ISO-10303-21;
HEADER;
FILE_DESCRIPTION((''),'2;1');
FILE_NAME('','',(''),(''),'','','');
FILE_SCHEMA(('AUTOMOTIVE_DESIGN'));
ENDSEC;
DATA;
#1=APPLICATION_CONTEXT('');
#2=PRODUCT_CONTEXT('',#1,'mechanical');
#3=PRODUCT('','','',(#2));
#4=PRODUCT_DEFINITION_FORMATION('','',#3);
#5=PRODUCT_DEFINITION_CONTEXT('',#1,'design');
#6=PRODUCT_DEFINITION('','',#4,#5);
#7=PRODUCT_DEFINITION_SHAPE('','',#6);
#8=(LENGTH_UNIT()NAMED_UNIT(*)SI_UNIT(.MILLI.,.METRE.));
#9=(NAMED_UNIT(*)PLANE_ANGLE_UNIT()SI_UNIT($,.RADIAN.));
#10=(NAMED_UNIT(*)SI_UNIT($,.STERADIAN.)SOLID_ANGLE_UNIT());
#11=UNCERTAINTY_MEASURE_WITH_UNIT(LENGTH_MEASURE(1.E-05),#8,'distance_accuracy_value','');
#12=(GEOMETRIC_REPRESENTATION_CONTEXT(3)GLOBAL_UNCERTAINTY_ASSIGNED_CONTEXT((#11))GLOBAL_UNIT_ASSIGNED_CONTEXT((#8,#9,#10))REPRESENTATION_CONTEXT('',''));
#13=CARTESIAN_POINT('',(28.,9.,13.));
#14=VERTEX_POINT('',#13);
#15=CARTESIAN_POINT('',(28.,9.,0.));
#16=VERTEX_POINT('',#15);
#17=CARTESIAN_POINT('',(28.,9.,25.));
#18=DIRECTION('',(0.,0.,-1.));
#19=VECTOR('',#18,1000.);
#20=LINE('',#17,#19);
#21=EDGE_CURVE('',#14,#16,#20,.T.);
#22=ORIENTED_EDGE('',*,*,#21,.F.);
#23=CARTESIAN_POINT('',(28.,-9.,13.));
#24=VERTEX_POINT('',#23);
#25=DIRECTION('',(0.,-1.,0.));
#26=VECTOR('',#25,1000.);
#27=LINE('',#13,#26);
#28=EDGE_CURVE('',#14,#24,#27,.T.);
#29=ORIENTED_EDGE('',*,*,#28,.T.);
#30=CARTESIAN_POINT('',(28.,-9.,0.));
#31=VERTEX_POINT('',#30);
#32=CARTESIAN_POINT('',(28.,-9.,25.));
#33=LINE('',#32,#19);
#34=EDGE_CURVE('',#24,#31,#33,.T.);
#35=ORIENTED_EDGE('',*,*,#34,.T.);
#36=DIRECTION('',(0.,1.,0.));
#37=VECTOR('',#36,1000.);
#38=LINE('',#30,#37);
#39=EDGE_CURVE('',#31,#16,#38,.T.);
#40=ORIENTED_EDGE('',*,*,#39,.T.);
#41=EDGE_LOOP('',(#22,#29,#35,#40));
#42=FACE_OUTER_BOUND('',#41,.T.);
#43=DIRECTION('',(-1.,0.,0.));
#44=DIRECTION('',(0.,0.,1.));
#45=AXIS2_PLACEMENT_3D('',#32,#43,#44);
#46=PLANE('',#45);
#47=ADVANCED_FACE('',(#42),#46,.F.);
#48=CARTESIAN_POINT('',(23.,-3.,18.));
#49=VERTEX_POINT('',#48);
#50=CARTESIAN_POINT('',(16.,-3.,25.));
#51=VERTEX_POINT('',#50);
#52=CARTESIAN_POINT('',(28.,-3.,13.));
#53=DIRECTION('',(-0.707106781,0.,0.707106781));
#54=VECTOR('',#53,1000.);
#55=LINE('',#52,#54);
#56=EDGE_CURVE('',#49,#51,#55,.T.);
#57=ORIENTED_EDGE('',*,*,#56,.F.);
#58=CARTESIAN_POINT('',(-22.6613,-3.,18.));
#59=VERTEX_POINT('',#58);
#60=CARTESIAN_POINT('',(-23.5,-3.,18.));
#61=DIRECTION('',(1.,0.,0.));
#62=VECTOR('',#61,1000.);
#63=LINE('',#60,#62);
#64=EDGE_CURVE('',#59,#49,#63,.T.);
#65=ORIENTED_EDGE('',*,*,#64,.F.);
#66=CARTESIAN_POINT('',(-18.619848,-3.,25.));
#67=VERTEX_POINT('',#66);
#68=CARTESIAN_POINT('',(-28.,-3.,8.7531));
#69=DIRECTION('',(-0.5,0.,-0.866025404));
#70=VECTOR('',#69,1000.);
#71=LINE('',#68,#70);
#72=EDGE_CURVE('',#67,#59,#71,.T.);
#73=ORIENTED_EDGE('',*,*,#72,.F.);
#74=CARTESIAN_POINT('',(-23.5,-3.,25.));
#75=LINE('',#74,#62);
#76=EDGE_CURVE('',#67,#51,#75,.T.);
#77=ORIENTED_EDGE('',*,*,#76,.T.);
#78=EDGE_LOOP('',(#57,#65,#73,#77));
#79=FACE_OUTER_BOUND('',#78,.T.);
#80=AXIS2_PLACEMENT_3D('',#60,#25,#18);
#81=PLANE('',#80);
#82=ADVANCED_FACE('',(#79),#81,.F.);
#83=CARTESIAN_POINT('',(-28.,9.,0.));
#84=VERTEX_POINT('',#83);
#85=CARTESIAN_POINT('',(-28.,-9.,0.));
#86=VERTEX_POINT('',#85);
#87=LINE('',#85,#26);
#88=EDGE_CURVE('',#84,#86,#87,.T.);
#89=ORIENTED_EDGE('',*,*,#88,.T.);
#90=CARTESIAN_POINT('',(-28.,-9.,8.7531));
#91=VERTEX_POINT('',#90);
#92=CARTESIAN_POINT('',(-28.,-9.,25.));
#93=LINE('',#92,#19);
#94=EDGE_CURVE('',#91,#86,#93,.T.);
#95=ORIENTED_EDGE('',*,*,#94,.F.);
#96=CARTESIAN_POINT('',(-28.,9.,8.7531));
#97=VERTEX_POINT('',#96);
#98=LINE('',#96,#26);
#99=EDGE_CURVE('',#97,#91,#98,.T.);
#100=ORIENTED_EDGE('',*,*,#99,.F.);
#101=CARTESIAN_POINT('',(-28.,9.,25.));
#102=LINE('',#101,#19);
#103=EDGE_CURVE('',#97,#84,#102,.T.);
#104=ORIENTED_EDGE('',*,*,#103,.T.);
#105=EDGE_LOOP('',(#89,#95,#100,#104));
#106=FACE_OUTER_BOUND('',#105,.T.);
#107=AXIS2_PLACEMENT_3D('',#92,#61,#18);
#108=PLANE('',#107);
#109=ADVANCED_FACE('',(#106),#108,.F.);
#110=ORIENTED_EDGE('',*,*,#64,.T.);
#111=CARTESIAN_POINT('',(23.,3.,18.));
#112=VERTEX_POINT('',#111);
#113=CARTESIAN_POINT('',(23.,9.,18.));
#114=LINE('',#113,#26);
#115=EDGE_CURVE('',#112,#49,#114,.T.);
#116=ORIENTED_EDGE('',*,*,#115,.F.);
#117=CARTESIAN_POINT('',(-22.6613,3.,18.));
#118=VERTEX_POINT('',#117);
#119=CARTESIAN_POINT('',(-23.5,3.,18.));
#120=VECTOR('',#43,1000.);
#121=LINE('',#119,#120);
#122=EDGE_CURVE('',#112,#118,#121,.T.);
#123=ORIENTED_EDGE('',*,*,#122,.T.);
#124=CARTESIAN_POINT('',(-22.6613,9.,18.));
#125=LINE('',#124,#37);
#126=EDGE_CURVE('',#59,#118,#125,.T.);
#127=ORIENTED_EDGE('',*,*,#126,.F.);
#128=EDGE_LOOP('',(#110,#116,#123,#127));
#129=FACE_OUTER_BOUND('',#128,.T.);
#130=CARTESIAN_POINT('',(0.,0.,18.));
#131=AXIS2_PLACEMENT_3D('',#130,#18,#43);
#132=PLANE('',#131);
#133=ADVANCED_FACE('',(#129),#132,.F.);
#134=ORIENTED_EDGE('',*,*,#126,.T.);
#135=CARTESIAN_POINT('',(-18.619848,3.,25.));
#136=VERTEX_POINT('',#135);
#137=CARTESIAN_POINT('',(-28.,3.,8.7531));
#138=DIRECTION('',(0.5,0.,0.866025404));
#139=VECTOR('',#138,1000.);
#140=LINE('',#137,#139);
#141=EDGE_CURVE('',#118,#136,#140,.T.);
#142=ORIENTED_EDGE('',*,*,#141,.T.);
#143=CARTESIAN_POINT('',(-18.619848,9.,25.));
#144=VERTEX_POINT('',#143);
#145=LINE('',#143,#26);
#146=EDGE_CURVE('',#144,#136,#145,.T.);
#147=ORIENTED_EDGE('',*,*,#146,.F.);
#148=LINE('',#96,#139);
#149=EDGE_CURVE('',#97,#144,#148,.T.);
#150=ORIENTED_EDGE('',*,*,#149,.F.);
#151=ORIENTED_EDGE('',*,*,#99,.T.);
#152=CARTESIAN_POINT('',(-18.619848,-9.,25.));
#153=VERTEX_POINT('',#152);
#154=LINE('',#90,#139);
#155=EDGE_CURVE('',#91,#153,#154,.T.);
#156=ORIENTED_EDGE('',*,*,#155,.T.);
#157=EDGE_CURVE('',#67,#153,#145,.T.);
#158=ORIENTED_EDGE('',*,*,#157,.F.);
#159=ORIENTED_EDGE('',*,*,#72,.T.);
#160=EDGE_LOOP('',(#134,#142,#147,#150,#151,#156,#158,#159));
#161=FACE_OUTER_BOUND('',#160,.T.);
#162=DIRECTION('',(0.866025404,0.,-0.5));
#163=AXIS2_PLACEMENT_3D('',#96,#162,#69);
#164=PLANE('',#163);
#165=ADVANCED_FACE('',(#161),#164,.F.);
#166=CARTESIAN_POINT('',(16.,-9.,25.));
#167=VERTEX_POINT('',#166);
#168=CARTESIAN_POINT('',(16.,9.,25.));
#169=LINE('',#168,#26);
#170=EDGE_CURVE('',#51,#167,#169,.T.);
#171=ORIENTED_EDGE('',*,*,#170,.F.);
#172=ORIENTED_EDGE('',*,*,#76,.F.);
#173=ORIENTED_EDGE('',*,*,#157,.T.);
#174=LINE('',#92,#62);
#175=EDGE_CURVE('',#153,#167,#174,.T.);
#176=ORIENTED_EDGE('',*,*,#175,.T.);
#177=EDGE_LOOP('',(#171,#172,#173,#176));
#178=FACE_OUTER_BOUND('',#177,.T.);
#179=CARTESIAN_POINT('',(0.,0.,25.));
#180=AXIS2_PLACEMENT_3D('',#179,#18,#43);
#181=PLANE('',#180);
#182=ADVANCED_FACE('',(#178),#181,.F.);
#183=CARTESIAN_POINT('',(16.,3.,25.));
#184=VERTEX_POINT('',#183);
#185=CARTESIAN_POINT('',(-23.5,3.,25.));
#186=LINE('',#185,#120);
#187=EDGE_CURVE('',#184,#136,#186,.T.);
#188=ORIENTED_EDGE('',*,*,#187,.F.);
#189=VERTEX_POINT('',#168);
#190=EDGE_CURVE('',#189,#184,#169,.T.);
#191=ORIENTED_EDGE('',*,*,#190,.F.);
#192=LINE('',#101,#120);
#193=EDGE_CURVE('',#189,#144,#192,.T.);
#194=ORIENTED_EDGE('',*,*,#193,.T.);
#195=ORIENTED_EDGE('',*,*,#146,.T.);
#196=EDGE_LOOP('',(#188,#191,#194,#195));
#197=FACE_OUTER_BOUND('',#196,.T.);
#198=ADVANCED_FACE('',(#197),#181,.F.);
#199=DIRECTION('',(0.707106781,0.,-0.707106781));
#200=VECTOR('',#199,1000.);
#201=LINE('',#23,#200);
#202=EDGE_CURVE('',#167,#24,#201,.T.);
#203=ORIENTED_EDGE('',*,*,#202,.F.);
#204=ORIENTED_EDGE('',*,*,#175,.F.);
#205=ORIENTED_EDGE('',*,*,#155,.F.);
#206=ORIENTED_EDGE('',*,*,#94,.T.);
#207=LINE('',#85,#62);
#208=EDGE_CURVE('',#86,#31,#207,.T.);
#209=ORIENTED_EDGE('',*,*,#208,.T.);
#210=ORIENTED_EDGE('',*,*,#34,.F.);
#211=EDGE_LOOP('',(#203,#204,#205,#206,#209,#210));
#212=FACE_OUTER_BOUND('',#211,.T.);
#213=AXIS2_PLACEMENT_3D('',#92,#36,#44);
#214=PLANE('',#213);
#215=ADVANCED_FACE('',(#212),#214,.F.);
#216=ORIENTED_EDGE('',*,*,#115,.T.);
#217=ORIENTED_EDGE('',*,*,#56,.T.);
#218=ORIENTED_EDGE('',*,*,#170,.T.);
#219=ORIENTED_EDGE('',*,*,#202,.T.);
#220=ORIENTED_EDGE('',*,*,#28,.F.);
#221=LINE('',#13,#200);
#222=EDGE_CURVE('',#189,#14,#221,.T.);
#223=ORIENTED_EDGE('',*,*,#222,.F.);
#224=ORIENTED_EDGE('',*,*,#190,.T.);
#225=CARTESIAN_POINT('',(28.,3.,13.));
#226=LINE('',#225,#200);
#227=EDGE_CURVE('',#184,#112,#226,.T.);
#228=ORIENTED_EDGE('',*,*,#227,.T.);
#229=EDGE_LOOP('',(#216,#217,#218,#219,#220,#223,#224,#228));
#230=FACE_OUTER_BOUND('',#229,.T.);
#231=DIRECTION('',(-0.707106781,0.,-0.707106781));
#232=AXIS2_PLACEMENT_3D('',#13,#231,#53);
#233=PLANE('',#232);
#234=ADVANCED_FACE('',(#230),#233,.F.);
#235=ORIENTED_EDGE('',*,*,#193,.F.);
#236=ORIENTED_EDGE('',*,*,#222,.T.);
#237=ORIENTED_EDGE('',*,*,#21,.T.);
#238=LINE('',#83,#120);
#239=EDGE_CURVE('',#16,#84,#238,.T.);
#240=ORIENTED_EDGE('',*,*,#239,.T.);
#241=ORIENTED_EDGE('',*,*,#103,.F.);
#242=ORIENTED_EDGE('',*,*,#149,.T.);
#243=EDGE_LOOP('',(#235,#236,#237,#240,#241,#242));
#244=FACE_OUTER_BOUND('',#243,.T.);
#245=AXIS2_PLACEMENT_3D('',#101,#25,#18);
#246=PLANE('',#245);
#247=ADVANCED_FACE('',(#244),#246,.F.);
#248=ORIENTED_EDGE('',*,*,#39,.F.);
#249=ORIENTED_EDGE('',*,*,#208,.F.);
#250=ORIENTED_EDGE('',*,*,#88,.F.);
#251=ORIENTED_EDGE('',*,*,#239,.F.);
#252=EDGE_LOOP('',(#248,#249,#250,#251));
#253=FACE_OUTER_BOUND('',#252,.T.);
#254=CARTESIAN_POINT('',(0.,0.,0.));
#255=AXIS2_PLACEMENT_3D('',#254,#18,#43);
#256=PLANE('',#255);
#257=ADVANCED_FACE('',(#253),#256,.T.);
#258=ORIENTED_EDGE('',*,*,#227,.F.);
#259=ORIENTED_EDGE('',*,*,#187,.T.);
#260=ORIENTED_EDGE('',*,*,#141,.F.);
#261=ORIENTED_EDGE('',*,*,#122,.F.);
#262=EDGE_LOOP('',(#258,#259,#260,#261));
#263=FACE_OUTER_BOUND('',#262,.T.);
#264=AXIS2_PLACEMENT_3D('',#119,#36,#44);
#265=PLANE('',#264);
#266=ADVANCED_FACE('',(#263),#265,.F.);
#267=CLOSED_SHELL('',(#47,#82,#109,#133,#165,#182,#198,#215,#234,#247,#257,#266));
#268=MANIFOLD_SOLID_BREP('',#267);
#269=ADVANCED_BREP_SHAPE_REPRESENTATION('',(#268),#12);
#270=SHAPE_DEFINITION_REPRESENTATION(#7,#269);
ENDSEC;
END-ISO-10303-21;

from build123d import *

# Parameters (mm, degrees)
BASE_PROFILE_SKETCH_W    = 56
BASE_PROFILE_SKETCH_H    = 18
BASE_BLOCK_DEPTH         = 25
ANGLED_CORNER_CUTS_DEPTH = 42.629316593
SLOT_SKETCH_W            = 47
SLOT_SKETCH_H            = 6
SLOT_47X6_DEPTH          = 7


with BuildPart() as part:
    # Base Profile Sketch → Base Block (new body)
    with BuildSketch(Plane.XY):
        Rectangle(BASE_PROFILE_SKETCH_W, BASE_PROFILE_SKETCH_H)
    extrude(amount=BASE_BLOCK_DEPTH)

    # Corner Cut Sketch → Angled Corner Cuts (cut, through all)
    with BuildSketch(Plane.XZ.offset(9)):
        Polygon((28, 13), (16, 25), (28, 25), align=None)
        Polygon((-28, 13), (-28, 8.753100352), (-18.619848115, 25), (-28, 25), align=None)
    extrude(amount=-ANGLED_CORNER_CUTS_DEPTH, mode=Mode.SUBTRACT)

    # Slot Sketch → Slot 47x6 (cut)
    with BuildSketch(Plane.XY.offset(25)):
        Rectangle(SLOT_SKETCH_W, SLOT_SKETCH_H)
    extrude(amount=-SLOT_47X6_DEPTH, mode=Mode.SUBTRACT)


solid = part.part
